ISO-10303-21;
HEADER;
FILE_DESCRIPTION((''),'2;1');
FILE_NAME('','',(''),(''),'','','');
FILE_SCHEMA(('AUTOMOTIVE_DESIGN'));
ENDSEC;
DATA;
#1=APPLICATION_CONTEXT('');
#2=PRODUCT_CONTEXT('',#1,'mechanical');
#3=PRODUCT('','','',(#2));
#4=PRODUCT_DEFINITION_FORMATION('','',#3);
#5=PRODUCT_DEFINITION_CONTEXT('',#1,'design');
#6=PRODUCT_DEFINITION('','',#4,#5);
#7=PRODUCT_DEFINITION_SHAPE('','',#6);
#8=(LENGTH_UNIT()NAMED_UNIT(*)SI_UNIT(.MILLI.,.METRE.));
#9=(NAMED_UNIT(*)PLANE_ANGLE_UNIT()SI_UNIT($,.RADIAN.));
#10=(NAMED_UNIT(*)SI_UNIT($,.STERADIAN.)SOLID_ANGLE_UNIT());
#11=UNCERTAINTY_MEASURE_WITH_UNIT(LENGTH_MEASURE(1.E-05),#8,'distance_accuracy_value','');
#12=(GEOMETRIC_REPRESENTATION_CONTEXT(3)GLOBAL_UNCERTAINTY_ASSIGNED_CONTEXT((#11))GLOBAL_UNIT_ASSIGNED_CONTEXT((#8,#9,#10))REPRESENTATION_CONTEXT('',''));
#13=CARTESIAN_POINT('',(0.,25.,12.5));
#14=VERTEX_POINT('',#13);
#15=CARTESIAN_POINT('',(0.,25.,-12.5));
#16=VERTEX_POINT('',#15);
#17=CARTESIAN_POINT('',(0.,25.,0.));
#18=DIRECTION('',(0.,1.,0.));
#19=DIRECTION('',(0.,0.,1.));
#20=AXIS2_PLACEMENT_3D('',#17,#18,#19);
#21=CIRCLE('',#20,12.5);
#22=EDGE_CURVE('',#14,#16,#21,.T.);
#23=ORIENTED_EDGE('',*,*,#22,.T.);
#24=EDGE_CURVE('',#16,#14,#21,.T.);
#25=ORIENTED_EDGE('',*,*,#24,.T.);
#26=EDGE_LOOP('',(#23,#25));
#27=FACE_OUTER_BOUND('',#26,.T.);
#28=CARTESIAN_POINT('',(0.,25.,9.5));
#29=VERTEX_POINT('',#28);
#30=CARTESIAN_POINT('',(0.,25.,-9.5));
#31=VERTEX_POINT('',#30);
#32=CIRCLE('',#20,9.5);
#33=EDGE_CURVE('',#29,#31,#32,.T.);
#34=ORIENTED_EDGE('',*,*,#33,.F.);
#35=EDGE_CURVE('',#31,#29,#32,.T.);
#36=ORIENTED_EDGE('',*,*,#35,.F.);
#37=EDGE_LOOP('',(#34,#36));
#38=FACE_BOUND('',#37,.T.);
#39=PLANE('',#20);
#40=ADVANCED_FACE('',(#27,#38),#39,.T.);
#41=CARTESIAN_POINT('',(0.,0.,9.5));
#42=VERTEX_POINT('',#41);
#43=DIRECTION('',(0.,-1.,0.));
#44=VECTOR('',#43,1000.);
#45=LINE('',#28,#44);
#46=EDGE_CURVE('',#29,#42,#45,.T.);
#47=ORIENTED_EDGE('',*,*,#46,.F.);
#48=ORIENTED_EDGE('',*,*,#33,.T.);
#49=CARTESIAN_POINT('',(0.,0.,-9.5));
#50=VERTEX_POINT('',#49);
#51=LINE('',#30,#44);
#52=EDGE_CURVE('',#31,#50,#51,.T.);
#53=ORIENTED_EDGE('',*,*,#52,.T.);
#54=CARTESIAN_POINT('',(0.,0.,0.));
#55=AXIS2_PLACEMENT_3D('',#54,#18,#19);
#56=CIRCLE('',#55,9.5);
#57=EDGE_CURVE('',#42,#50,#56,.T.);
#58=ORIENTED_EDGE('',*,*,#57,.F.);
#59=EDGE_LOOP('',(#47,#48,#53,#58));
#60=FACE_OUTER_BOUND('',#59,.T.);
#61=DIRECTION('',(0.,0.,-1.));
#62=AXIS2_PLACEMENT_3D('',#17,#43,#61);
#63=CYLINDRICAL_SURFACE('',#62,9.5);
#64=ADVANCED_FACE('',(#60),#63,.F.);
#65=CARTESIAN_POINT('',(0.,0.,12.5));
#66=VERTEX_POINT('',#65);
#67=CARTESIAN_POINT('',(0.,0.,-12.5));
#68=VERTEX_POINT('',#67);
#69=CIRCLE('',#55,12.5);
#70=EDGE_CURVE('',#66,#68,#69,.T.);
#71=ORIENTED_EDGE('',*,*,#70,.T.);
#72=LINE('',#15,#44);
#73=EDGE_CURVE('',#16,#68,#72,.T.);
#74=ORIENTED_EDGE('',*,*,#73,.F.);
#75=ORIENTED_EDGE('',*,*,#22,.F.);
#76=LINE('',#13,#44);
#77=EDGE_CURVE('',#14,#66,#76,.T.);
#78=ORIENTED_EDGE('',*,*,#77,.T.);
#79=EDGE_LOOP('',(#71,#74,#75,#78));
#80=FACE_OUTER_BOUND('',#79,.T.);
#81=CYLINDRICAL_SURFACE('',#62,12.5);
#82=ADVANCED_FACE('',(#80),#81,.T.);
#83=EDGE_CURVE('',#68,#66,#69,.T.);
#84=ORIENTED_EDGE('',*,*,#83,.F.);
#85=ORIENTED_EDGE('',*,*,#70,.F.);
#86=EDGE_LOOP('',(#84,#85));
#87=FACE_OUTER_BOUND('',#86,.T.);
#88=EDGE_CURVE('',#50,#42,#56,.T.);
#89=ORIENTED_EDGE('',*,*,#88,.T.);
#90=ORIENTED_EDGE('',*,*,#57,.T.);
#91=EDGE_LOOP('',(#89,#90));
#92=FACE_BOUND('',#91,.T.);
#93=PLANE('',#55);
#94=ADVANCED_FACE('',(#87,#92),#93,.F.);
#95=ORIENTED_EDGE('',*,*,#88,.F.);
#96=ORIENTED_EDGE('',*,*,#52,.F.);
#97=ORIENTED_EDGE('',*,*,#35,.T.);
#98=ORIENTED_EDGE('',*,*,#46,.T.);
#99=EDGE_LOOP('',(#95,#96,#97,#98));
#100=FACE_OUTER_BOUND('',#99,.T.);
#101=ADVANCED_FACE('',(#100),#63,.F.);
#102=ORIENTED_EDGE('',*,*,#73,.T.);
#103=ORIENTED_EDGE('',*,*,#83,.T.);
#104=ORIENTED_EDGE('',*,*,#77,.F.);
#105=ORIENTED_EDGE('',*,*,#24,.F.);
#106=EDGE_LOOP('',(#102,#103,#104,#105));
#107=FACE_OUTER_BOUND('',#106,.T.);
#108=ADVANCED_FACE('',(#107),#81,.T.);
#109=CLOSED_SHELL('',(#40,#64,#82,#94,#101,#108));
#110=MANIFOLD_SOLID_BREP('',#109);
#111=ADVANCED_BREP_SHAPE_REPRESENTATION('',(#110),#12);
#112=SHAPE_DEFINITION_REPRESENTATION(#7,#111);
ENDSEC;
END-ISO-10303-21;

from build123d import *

# Parameters (mm, degrees)
BUSHING_PROFILE_25X_19_R   = 12.5
BUSHING_PROFILE_25X_19_R_2 = 9.5
BUSHING_BODY_L25_DEPTH     = 25


with BuildPart() as part:
    # Bushing Profile Ø25xØ19 → Bushing Body L25 (new body)
    with BuildSketch(Plane(origin=(0, 0, 0), x_dir=(1, 0, 0), z_dir=(0, 1, 0))):
        with Locations(Location((0, 0, 0), (0, 0, 270))):
            Circle(BUSHING_PROFILE_25X_19_R)
        with Locations(Location((0, 0, 0), (0, 0, 270))):
            Circle(BUSHING_PROFILE_25X_19_R_2, mode=Mode.SUBTRACT)
    extrude(amount=BUSHING_BODY_L25_DEPTH)


solid = part.part
